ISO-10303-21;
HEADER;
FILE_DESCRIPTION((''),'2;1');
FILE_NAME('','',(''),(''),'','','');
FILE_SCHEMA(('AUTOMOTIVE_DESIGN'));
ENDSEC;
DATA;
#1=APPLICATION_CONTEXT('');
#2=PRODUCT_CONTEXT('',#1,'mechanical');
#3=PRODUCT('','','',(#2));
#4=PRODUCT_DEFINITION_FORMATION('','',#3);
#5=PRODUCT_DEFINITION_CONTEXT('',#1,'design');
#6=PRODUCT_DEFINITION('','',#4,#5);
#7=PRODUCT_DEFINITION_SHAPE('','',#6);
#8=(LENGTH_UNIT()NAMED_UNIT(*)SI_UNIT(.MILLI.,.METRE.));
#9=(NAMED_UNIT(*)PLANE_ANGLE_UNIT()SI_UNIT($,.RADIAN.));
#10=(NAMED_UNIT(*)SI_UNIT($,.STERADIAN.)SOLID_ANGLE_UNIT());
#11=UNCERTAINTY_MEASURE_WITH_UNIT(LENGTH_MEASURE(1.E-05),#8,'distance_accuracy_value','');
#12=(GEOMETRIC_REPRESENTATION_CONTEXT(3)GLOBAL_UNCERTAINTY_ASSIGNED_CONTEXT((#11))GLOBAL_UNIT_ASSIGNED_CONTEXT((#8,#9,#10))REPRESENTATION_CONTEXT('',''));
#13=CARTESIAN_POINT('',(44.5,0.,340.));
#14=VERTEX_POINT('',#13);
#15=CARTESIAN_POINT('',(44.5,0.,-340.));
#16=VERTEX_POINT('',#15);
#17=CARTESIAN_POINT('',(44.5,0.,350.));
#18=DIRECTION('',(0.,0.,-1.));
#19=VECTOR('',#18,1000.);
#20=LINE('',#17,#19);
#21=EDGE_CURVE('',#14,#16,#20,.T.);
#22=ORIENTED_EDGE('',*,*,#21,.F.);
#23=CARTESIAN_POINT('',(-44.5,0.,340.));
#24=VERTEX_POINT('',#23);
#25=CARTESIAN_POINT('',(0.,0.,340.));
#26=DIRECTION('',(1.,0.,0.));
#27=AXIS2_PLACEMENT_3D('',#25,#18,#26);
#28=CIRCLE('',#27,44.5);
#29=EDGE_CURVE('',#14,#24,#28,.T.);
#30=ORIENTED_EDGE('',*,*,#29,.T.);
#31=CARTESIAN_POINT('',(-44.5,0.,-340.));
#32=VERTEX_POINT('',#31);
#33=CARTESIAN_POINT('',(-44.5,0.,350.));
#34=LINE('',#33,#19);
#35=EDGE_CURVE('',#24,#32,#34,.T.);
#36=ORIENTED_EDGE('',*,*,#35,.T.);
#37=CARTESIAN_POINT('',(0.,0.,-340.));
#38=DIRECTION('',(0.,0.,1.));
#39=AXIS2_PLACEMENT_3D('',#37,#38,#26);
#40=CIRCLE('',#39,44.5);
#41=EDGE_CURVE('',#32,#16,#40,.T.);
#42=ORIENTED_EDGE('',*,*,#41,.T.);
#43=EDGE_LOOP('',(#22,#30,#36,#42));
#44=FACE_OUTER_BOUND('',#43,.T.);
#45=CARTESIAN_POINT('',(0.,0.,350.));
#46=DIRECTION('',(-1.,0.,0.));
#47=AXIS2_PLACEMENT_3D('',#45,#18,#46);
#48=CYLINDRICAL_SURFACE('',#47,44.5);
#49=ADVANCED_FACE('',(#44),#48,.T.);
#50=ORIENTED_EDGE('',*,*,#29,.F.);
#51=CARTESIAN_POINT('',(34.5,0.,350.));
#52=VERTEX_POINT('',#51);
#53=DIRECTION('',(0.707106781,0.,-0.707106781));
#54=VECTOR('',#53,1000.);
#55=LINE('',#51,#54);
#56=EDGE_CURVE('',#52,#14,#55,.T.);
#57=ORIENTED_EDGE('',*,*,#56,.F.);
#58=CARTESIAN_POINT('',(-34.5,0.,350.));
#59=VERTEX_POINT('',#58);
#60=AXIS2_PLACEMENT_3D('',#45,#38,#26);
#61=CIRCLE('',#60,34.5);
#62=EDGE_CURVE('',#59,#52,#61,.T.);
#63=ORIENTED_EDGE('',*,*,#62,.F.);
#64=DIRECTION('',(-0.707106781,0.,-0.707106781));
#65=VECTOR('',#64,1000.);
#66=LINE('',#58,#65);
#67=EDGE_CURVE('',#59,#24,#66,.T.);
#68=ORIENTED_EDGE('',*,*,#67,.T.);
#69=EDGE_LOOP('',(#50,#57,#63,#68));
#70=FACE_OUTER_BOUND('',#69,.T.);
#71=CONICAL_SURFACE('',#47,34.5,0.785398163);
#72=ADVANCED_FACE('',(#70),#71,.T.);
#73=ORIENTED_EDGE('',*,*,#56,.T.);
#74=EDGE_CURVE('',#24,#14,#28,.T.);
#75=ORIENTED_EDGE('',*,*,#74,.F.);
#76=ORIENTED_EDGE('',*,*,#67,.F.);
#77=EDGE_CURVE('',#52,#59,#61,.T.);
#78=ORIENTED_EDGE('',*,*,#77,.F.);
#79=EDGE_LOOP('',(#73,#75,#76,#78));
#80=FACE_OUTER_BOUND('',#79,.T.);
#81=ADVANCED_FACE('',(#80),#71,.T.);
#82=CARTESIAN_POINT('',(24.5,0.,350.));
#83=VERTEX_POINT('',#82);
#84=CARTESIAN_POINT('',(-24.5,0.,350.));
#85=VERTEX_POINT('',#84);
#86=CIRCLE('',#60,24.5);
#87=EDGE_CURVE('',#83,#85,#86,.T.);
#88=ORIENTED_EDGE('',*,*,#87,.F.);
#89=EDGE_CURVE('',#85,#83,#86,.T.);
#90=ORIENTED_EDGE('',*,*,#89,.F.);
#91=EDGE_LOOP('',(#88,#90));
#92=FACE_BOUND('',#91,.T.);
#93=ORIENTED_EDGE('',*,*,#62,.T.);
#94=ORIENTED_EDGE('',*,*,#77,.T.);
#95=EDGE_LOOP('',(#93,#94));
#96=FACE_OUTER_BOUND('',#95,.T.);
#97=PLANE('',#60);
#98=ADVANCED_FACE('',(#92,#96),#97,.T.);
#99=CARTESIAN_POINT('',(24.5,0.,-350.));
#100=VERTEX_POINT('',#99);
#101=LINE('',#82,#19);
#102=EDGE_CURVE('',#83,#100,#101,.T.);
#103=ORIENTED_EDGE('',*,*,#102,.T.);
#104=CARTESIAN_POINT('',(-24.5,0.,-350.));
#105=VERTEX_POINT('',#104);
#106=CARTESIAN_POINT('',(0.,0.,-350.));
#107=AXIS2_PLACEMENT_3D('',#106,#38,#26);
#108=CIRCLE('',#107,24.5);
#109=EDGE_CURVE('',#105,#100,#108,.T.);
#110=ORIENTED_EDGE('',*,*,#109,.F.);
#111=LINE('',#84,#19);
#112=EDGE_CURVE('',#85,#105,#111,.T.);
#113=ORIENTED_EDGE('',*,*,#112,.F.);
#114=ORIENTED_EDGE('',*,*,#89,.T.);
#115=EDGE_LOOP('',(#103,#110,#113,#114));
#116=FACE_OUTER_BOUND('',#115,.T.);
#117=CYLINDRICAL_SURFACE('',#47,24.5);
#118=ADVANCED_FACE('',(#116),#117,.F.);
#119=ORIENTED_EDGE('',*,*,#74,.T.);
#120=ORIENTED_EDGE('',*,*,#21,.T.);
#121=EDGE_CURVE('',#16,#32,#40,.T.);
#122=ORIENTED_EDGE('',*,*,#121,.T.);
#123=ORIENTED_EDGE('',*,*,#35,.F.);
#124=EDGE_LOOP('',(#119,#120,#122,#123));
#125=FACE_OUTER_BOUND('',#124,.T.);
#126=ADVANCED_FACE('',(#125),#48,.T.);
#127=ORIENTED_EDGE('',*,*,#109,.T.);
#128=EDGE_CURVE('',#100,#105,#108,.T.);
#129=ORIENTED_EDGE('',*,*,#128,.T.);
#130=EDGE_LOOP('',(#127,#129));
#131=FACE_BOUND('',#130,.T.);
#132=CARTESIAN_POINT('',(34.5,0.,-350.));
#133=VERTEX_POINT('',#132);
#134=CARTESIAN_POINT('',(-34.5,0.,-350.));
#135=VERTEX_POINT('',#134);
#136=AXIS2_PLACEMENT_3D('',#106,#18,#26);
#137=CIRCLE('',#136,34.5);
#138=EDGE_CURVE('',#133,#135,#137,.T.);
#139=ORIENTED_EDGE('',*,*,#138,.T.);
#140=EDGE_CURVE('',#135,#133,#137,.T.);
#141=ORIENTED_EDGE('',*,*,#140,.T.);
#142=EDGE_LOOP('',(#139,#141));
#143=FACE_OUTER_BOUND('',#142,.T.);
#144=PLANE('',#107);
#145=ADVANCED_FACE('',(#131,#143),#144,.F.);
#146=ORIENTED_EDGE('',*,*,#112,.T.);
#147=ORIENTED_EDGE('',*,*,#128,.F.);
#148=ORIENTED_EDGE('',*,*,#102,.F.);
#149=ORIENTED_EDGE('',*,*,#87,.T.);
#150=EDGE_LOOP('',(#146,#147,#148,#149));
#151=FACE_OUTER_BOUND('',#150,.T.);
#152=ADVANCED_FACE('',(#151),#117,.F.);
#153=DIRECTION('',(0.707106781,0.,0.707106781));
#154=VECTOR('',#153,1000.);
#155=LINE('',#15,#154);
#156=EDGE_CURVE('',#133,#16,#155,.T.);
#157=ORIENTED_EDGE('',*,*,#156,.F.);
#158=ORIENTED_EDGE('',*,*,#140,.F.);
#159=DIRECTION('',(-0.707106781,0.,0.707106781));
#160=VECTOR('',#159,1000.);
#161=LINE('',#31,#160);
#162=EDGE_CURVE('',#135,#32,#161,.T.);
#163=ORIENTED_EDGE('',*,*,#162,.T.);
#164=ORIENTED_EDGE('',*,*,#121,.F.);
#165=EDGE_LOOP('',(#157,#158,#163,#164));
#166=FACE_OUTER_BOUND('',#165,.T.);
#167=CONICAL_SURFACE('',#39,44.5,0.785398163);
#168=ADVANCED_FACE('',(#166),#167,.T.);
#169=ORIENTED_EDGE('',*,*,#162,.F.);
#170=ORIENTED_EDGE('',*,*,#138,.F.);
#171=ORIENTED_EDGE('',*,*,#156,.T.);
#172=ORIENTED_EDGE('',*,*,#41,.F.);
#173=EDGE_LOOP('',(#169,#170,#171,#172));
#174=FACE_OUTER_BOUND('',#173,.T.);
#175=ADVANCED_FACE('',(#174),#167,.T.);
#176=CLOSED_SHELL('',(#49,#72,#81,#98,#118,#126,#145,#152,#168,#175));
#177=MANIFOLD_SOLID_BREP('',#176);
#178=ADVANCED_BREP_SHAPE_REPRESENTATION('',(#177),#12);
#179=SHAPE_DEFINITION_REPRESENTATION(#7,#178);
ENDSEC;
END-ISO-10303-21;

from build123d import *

# Parameters (mm, degrees)
SKETCH1_R           = 44.5
SKETCH1_R_2         = 24.5
EXTRUDE_THIN1_DEPTH = 350
CHAMFER1_SIZE       = 10


with BuildPart() as part:
    # Sketch1 → Extrude-Thin1 (new, symmetric)
    with BuildSketch(Plane.XY):
        Circle(SKETCH1_R)
        Circle(SKETCH1_R_2, mode=Mode.SUBTRACT)
    extrude(amount=EXTRUDE_THIN1_DEPTH, both=True)

    # Chamfer1
    chamfer1_edges = [part.edges().sort_by_distance(p)[0] for p in [
        (-44.5, 0, -350),
        (-44.5, 0, 350),
    ]]
    chamfer(chamfer1_edges, length=CHAMFER1_SIZE)


solid = part.part
